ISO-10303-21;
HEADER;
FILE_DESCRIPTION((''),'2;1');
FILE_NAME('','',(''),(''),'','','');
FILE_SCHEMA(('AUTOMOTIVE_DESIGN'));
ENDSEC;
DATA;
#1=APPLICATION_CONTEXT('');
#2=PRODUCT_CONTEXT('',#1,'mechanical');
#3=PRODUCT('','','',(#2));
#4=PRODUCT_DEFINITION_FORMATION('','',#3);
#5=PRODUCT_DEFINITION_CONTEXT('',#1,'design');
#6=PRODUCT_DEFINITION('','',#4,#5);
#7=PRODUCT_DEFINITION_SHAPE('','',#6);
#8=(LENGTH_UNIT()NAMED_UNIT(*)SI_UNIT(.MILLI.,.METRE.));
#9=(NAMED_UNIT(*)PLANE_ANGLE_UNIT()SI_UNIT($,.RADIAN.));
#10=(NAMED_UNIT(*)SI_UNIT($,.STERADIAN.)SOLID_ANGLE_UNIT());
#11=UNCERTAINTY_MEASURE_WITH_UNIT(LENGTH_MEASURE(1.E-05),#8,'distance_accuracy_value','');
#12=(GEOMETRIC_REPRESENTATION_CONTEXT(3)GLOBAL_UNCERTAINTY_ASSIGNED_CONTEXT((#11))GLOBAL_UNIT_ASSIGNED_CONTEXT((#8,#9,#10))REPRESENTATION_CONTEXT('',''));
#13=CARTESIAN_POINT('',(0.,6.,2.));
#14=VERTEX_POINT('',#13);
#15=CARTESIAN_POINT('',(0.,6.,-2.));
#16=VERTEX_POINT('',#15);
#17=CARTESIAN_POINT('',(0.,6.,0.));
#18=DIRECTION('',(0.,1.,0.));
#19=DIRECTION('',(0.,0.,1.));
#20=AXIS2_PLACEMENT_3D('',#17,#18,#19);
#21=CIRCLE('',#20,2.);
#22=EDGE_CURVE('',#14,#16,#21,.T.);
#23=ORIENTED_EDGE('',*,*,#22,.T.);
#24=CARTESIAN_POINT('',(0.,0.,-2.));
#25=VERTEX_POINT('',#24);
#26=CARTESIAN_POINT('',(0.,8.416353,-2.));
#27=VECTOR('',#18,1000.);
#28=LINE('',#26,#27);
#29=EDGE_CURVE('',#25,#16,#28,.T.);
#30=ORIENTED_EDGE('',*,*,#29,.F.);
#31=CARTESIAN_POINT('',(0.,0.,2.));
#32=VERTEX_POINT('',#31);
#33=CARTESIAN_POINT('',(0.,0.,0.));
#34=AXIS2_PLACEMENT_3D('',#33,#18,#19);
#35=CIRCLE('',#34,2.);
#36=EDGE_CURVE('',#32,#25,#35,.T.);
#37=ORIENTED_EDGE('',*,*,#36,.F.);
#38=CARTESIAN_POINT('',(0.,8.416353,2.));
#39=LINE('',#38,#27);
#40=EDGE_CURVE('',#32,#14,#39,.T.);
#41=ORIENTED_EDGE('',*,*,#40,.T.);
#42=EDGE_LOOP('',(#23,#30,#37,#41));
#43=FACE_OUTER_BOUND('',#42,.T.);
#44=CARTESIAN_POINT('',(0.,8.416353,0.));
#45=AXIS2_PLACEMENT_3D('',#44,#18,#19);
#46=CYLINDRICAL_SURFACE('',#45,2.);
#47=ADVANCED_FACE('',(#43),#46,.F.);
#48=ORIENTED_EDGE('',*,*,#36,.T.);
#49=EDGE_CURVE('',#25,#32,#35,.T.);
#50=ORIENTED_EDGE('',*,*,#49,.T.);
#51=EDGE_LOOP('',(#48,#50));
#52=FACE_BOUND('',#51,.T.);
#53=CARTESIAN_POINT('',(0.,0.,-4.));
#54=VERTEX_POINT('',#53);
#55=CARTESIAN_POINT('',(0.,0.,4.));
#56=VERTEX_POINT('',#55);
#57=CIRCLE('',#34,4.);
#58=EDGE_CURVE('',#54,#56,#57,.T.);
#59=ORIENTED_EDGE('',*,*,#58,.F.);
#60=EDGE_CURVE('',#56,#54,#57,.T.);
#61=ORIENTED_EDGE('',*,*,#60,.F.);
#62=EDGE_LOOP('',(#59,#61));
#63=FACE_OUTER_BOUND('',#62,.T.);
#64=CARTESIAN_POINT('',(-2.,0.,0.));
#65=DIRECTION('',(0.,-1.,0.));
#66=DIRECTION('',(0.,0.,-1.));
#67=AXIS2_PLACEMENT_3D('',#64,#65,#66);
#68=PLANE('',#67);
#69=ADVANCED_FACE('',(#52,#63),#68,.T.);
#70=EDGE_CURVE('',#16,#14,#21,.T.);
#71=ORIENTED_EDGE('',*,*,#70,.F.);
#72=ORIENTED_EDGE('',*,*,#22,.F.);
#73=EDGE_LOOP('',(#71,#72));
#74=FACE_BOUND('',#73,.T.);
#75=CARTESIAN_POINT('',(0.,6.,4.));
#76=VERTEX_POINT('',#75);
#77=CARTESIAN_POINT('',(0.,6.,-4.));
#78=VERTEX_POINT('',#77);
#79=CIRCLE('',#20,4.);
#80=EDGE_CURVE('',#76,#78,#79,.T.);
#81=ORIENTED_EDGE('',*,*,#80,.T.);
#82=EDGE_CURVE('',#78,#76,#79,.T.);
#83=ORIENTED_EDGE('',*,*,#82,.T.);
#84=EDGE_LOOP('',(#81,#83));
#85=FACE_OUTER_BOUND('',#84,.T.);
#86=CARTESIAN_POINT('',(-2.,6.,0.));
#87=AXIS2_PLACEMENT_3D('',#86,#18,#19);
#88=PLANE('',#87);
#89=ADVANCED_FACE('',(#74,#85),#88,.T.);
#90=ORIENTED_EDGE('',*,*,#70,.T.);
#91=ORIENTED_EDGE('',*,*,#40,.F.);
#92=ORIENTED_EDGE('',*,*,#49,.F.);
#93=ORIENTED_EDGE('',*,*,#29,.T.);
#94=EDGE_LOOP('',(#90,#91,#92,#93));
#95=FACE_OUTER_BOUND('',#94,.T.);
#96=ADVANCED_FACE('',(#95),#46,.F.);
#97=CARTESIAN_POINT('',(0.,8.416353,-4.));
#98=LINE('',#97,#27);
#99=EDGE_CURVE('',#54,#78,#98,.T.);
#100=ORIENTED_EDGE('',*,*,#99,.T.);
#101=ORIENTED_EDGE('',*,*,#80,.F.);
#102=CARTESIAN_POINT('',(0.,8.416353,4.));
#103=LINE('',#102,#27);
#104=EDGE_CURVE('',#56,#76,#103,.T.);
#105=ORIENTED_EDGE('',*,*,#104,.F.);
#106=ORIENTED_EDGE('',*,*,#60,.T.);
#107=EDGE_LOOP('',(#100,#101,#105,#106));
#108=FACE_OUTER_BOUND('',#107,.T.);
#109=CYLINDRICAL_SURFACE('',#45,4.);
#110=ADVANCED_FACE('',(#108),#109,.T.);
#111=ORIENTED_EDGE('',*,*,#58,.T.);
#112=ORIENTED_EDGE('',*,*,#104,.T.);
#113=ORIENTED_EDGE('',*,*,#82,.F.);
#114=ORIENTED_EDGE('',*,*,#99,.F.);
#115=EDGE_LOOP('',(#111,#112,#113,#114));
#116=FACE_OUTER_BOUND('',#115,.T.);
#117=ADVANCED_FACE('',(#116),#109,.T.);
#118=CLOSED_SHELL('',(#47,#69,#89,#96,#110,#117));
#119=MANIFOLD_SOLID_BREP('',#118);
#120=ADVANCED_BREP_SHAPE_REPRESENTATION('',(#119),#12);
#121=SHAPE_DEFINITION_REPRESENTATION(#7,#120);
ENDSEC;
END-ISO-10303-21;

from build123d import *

# Parameters (mm, degrees)
SKETCH1_W = 2
SKETCH1_H = 6


with BuildPart() as part:
    # Sketch1 → Revolve1 (revolve)
    with BuildSketch(Plane.XY, mode=Mode.PRIVATE) as revolve1_sk:
        with Locations((-3, 3)):
            Rectangle(SKETCH1_W, SKETCH1_H)
    revolve(revolve1_sk.sketch.rotate(Axis((0, 8.416352699, 0), (0, -1, 0)), 270), axis=Axis((0, 8.416352699, 0), (0, -1, 0)))


solid = part.part
